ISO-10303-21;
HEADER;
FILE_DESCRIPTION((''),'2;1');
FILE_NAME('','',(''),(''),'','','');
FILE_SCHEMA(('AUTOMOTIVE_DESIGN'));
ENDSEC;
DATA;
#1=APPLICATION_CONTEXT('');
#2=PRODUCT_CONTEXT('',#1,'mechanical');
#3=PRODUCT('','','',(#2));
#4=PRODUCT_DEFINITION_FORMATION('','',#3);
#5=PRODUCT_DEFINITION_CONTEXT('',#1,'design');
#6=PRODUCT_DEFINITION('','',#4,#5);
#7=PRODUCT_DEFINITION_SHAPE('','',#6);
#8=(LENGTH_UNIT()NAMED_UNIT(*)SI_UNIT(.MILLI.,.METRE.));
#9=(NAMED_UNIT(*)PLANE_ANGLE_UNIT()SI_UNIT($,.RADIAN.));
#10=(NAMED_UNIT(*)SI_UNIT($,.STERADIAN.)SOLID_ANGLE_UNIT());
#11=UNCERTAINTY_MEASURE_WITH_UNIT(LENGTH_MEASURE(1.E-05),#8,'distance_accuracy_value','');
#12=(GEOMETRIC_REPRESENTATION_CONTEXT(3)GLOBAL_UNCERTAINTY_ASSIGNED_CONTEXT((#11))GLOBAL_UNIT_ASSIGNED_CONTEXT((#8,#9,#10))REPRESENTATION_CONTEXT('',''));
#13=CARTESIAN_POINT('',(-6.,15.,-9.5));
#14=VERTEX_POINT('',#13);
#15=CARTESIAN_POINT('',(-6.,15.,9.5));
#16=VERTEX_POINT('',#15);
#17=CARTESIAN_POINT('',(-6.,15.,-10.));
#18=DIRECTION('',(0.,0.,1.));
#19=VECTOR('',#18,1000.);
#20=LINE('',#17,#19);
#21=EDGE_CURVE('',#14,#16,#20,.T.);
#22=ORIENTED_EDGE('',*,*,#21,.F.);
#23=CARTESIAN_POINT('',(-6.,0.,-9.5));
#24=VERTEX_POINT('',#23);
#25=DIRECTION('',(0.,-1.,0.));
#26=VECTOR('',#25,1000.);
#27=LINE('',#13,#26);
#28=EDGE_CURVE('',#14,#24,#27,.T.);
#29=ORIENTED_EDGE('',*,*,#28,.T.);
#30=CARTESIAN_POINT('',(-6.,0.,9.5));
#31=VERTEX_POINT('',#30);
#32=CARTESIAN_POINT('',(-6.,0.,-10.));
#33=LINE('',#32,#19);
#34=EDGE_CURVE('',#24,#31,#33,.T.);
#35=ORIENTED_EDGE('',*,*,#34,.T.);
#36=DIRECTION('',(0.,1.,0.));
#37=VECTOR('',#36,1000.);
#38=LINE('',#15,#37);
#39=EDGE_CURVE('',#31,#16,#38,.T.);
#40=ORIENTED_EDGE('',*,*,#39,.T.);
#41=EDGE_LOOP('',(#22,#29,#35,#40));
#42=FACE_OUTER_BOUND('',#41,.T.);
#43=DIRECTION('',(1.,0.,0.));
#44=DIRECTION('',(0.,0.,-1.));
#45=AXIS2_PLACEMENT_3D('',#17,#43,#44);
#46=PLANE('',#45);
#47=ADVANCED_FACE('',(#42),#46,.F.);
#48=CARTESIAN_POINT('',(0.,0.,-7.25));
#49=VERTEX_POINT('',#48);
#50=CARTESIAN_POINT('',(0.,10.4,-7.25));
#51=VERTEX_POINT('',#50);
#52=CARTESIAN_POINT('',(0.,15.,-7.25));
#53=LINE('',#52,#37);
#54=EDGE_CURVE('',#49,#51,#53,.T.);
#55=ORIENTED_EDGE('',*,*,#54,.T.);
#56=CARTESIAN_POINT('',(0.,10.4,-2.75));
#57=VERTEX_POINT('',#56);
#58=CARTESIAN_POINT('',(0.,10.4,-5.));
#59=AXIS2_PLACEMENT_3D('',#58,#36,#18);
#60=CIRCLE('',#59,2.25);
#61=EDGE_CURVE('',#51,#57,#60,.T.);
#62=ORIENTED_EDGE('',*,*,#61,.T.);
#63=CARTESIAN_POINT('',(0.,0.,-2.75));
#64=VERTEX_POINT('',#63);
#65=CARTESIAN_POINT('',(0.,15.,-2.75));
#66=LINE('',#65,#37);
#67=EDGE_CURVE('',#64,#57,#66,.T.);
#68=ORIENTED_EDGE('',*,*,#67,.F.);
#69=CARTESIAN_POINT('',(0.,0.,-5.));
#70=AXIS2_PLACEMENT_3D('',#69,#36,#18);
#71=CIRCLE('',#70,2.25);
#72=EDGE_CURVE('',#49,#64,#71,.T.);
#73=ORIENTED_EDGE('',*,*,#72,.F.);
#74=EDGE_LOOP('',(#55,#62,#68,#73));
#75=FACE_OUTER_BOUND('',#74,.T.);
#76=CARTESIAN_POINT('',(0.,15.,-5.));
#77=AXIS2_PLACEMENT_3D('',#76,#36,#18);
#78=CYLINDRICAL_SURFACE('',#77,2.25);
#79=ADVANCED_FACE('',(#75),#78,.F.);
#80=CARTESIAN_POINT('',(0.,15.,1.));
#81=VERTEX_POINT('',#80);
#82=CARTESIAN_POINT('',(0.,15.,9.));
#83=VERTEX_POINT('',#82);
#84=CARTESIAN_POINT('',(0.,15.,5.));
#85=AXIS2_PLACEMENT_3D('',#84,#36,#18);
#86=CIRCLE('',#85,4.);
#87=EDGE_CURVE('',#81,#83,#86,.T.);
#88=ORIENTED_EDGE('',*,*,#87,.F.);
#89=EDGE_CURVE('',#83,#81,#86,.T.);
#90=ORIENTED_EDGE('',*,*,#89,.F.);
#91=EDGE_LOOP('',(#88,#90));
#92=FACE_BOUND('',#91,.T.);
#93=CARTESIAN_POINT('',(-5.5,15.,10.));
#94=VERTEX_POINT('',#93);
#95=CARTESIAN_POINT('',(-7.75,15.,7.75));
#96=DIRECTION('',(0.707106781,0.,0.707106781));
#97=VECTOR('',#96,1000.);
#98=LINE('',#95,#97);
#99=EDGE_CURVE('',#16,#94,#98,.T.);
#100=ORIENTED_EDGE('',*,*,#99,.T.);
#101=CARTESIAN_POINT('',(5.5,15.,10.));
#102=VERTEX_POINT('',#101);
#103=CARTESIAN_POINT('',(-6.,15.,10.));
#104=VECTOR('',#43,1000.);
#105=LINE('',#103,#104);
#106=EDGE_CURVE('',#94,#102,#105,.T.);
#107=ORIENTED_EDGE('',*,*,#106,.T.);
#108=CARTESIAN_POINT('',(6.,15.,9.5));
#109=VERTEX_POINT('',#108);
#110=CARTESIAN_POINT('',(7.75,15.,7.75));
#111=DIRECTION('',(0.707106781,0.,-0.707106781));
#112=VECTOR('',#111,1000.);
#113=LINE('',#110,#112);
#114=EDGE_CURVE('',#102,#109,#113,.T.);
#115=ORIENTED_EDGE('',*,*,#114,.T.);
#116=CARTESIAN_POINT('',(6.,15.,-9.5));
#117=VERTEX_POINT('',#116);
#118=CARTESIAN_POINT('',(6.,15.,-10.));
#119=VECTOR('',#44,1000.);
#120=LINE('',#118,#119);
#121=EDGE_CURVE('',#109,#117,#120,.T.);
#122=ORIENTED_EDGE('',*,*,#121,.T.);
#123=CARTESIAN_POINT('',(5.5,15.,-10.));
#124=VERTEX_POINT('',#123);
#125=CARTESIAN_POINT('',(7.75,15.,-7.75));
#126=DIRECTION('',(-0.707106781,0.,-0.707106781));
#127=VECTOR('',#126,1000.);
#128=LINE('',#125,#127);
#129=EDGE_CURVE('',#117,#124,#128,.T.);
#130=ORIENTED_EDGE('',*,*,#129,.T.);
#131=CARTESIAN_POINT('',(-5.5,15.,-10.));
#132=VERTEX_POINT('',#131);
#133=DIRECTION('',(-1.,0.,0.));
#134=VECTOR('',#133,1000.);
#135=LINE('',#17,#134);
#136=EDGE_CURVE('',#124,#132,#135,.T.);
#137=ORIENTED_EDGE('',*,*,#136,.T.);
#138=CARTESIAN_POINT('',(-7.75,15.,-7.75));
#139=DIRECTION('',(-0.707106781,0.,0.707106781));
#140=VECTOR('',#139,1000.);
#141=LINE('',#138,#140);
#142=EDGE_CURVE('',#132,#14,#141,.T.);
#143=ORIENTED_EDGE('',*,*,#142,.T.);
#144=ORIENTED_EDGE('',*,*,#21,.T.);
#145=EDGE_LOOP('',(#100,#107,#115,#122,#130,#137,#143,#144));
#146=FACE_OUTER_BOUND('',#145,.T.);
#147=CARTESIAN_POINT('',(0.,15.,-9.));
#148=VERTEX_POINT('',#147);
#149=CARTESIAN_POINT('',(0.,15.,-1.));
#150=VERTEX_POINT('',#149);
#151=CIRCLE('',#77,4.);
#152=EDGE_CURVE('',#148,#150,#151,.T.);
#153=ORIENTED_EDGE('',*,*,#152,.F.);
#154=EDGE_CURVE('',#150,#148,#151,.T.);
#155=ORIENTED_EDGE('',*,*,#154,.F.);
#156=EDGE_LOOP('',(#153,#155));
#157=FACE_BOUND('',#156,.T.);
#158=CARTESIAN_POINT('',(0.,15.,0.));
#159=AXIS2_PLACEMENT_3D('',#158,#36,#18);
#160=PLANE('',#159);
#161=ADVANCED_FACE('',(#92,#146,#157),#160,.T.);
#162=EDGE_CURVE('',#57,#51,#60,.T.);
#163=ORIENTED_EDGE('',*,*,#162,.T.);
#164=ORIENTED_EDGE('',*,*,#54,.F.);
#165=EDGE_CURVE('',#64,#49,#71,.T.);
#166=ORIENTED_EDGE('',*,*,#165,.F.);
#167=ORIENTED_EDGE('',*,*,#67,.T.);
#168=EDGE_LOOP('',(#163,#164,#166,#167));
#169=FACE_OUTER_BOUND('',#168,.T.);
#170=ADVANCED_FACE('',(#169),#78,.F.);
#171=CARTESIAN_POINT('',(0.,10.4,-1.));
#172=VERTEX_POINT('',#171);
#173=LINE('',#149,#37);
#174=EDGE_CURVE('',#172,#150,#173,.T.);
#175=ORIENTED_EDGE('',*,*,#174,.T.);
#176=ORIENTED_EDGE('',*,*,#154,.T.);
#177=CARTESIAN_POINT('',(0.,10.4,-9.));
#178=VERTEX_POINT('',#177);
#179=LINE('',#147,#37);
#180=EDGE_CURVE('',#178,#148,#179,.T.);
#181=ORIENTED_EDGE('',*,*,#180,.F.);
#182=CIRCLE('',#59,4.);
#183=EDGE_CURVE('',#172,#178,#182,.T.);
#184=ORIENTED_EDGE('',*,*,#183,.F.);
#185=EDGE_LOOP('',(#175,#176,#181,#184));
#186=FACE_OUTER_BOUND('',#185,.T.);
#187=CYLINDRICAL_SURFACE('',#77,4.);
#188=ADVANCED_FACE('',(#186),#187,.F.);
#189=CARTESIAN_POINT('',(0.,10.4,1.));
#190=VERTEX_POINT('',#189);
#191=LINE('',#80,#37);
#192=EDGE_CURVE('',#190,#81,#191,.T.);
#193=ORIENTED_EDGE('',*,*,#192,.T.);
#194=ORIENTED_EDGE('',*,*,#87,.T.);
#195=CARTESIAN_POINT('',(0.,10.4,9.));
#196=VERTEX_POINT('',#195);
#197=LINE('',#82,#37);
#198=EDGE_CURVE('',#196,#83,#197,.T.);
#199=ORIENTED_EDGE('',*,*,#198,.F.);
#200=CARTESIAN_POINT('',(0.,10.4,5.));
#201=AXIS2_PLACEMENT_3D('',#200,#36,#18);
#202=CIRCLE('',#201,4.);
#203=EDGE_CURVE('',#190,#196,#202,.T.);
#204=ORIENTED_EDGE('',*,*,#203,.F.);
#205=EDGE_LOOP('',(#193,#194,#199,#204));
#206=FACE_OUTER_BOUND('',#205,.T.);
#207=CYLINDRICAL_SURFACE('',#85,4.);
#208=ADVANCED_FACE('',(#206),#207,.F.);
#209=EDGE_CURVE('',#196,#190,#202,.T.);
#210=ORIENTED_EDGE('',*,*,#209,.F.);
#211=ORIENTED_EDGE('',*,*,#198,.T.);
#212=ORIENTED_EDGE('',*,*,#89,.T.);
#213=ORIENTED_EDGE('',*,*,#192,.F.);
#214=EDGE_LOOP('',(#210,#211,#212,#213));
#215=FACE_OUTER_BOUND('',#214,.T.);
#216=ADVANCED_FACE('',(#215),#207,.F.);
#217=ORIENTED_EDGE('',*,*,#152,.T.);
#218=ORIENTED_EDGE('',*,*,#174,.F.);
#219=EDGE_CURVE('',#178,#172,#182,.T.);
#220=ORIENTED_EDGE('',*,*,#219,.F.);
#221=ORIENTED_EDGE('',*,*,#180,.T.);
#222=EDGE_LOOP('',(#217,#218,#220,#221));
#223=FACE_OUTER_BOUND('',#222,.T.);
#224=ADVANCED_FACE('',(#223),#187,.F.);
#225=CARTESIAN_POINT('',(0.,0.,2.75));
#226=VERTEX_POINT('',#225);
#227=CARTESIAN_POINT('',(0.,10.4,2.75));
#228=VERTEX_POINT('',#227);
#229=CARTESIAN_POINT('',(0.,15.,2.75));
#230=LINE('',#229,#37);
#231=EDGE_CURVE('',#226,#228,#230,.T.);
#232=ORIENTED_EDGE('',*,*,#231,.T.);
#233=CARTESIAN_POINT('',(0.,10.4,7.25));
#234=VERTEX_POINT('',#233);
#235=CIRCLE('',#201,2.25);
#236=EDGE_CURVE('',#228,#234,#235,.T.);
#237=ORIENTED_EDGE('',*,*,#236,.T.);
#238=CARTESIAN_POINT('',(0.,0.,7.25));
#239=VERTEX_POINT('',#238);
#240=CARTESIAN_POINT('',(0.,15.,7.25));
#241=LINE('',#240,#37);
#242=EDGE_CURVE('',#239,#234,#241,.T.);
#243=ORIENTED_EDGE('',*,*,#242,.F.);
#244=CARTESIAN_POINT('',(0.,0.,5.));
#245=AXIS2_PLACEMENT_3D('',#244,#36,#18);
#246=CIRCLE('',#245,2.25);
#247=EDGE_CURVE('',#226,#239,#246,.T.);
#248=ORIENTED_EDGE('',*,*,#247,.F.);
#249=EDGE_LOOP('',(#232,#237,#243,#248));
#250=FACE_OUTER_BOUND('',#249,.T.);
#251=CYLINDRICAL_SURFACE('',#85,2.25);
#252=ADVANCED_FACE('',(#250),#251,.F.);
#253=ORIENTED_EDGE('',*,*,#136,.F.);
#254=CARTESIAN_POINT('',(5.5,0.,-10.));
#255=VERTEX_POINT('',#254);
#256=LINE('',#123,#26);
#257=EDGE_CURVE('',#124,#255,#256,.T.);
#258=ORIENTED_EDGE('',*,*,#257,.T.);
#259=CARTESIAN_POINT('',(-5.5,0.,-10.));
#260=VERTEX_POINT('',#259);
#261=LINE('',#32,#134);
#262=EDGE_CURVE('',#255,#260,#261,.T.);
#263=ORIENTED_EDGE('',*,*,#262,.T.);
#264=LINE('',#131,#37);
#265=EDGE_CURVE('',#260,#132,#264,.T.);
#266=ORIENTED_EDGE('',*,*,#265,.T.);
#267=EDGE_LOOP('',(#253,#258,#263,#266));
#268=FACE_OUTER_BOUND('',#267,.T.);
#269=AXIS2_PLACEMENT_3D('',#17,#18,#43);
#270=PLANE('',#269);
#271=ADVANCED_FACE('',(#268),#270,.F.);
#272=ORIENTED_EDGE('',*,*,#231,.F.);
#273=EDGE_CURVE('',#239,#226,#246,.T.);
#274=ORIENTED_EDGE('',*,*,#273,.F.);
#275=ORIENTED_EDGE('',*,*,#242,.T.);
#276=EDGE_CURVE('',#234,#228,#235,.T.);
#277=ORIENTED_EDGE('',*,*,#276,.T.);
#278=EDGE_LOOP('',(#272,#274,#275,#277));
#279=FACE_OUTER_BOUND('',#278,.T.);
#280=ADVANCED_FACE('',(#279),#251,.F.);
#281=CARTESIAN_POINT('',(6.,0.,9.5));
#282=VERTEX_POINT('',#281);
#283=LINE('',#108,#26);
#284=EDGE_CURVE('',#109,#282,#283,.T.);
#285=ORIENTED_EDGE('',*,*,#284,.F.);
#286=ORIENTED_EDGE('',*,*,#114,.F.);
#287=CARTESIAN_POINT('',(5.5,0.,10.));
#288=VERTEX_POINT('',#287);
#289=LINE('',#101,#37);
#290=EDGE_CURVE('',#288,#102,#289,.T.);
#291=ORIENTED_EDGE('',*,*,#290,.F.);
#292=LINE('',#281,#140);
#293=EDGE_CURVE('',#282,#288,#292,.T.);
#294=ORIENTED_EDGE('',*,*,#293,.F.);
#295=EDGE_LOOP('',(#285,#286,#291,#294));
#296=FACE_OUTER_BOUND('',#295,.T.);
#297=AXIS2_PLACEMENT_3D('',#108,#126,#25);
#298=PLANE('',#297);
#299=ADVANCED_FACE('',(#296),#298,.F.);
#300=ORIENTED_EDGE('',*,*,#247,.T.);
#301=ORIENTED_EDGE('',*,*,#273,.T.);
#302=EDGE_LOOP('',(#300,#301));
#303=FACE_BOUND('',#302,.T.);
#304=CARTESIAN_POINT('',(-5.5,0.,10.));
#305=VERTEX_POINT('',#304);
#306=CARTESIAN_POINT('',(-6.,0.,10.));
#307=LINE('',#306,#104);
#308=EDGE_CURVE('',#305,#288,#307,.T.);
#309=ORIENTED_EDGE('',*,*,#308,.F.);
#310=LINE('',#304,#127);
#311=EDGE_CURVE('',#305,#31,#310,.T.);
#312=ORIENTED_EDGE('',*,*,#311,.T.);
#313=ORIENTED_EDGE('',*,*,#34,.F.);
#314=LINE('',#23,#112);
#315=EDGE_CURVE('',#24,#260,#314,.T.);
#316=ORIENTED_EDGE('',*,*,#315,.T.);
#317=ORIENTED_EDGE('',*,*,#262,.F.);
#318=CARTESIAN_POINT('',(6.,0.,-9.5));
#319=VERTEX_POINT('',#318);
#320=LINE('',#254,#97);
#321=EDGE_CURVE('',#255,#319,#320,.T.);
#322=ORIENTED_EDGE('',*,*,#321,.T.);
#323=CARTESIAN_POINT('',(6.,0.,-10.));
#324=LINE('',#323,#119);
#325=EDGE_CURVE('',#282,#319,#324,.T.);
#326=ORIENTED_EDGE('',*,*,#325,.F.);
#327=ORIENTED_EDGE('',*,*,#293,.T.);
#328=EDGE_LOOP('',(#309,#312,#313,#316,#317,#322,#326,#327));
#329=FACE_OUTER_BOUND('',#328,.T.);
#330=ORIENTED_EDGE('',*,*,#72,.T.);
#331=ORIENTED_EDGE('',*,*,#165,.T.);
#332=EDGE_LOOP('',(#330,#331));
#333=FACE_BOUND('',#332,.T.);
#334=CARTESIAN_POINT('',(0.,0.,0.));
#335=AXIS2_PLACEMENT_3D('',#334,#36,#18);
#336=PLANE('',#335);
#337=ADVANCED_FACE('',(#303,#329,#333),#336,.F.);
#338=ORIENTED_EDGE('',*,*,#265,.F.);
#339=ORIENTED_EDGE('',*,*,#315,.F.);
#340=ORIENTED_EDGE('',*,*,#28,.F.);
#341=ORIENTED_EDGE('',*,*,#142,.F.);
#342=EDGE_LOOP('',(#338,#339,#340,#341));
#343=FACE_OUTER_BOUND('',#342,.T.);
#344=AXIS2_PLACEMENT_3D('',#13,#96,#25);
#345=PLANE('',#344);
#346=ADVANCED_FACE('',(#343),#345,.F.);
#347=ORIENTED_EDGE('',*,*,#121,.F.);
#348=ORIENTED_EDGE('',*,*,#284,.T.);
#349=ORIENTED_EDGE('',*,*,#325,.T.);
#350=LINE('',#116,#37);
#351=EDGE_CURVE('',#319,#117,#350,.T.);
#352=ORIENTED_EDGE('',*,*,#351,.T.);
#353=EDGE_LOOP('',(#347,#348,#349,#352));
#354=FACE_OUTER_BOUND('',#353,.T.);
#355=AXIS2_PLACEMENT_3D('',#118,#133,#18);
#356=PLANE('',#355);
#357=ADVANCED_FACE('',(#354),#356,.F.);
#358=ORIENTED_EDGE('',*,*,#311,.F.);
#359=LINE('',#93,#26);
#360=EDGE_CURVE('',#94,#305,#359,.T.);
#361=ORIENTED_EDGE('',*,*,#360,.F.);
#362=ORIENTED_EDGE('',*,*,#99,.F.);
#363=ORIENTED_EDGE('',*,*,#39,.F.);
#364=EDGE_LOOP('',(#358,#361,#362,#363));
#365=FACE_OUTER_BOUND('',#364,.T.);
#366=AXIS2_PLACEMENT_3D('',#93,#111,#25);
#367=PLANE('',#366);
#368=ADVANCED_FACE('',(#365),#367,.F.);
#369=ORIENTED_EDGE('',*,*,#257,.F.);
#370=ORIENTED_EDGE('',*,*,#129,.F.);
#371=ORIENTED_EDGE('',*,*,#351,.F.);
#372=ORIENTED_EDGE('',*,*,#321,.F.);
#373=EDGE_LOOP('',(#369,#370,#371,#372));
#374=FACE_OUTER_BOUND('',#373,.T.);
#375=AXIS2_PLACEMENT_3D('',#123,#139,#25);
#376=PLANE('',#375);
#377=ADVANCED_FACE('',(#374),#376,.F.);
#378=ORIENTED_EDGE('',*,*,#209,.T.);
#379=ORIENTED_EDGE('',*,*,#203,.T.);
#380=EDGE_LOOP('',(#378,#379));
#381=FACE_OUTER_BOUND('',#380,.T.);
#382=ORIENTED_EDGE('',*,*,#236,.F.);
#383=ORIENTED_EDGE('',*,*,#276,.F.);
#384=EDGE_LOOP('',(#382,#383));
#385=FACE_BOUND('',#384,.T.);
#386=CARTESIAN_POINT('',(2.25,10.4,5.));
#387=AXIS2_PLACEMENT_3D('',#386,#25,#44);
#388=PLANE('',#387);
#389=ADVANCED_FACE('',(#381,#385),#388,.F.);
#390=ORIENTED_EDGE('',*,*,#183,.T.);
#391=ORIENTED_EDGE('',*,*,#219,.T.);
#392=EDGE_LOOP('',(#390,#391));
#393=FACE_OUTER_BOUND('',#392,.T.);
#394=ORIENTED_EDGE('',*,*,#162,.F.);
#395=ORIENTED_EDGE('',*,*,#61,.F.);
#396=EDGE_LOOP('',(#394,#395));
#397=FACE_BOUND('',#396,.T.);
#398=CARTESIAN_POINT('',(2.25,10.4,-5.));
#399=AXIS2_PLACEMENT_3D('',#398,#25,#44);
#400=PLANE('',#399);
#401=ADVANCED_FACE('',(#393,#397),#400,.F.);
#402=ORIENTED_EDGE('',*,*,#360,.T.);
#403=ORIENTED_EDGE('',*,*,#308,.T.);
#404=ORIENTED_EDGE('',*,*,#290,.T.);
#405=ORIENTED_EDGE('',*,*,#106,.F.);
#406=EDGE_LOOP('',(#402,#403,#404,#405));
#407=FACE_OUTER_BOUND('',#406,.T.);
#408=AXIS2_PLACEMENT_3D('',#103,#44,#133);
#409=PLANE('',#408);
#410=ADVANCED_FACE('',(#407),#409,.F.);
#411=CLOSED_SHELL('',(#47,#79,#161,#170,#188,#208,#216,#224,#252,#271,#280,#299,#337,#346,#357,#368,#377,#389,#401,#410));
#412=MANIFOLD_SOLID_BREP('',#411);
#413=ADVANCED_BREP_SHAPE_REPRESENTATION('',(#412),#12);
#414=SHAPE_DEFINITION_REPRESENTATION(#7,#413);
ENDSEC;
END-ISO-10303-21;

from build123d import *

# Parameters (mm, degrees)
SKETCH_1_W                = 12
SKETCH_1_H                = 20
EXTRUDE_1_DEPTH           = 15
HOLE_WIZARD_1_D           = 4.5
HOLE_WIZARD_1_DEPTH       = 20
HOLE_WIZARD_1_CBORE_D     = 8
HOLE_WIZARD_1_CBORE_DEPTH = 4.6
HOLE_WIZARD_1_TIP         = 1.351936393
CHAMFER_1_SIZE            = 0.5


with BuildPart() as part:
    # 草图1 → 凸台-拉伸1 (new body)
    with BuildSketch(Plane(origin=(0, 0, 0), x_dir=(1, 0, 0), z_dir=(0, 1, 0))):
        Rectangle(SKETCH_1_W, SKETCH_1_H)
    extrude(amount=EXTRUDE_1_DEPTH)

    # 打孔尺寸(%根据)内六角圆柱头螺钉的类型1
    with Locations(Plane(origin=(0, 15, 0), x_dir=(1, 0, 0), z_dir=(0, 1, 0))):
        with Locations((0, 5), (0, -5)):
            CounterBoreHole(HOLE_WIZARD_1_D / 2, HOLE_WIZARD_1_CBORE_D / 2, HOLE_WIZARD_1_CBORE_DEPTH, depth=HOLE_WIZARD_1_DEPTH)
            with Locations((0, 0, -(HOLE_WIZARD_1_DEPTH + HOLE_WIZARD_1_TIP / 2))):  # 118° drill point
                Cone(0, HOLE_WIZARD_1_D / 2, HOLE_WIZARD_1_TIP, mode=Mode.SUBTRACT)

    # 倒角1
    chamfer_1_edges = [part.edges().sort_by_distance(p)[0] for p in [
        (6, 7.5, 10),
        (-6, 7.5, 10),
        (-6, 7.5, -10),
        (6, 7.5, -10),
    ]]
    chamfer(chamfer_1_edges, length=CHAMFER_1_SIZE)


solid = part.part
